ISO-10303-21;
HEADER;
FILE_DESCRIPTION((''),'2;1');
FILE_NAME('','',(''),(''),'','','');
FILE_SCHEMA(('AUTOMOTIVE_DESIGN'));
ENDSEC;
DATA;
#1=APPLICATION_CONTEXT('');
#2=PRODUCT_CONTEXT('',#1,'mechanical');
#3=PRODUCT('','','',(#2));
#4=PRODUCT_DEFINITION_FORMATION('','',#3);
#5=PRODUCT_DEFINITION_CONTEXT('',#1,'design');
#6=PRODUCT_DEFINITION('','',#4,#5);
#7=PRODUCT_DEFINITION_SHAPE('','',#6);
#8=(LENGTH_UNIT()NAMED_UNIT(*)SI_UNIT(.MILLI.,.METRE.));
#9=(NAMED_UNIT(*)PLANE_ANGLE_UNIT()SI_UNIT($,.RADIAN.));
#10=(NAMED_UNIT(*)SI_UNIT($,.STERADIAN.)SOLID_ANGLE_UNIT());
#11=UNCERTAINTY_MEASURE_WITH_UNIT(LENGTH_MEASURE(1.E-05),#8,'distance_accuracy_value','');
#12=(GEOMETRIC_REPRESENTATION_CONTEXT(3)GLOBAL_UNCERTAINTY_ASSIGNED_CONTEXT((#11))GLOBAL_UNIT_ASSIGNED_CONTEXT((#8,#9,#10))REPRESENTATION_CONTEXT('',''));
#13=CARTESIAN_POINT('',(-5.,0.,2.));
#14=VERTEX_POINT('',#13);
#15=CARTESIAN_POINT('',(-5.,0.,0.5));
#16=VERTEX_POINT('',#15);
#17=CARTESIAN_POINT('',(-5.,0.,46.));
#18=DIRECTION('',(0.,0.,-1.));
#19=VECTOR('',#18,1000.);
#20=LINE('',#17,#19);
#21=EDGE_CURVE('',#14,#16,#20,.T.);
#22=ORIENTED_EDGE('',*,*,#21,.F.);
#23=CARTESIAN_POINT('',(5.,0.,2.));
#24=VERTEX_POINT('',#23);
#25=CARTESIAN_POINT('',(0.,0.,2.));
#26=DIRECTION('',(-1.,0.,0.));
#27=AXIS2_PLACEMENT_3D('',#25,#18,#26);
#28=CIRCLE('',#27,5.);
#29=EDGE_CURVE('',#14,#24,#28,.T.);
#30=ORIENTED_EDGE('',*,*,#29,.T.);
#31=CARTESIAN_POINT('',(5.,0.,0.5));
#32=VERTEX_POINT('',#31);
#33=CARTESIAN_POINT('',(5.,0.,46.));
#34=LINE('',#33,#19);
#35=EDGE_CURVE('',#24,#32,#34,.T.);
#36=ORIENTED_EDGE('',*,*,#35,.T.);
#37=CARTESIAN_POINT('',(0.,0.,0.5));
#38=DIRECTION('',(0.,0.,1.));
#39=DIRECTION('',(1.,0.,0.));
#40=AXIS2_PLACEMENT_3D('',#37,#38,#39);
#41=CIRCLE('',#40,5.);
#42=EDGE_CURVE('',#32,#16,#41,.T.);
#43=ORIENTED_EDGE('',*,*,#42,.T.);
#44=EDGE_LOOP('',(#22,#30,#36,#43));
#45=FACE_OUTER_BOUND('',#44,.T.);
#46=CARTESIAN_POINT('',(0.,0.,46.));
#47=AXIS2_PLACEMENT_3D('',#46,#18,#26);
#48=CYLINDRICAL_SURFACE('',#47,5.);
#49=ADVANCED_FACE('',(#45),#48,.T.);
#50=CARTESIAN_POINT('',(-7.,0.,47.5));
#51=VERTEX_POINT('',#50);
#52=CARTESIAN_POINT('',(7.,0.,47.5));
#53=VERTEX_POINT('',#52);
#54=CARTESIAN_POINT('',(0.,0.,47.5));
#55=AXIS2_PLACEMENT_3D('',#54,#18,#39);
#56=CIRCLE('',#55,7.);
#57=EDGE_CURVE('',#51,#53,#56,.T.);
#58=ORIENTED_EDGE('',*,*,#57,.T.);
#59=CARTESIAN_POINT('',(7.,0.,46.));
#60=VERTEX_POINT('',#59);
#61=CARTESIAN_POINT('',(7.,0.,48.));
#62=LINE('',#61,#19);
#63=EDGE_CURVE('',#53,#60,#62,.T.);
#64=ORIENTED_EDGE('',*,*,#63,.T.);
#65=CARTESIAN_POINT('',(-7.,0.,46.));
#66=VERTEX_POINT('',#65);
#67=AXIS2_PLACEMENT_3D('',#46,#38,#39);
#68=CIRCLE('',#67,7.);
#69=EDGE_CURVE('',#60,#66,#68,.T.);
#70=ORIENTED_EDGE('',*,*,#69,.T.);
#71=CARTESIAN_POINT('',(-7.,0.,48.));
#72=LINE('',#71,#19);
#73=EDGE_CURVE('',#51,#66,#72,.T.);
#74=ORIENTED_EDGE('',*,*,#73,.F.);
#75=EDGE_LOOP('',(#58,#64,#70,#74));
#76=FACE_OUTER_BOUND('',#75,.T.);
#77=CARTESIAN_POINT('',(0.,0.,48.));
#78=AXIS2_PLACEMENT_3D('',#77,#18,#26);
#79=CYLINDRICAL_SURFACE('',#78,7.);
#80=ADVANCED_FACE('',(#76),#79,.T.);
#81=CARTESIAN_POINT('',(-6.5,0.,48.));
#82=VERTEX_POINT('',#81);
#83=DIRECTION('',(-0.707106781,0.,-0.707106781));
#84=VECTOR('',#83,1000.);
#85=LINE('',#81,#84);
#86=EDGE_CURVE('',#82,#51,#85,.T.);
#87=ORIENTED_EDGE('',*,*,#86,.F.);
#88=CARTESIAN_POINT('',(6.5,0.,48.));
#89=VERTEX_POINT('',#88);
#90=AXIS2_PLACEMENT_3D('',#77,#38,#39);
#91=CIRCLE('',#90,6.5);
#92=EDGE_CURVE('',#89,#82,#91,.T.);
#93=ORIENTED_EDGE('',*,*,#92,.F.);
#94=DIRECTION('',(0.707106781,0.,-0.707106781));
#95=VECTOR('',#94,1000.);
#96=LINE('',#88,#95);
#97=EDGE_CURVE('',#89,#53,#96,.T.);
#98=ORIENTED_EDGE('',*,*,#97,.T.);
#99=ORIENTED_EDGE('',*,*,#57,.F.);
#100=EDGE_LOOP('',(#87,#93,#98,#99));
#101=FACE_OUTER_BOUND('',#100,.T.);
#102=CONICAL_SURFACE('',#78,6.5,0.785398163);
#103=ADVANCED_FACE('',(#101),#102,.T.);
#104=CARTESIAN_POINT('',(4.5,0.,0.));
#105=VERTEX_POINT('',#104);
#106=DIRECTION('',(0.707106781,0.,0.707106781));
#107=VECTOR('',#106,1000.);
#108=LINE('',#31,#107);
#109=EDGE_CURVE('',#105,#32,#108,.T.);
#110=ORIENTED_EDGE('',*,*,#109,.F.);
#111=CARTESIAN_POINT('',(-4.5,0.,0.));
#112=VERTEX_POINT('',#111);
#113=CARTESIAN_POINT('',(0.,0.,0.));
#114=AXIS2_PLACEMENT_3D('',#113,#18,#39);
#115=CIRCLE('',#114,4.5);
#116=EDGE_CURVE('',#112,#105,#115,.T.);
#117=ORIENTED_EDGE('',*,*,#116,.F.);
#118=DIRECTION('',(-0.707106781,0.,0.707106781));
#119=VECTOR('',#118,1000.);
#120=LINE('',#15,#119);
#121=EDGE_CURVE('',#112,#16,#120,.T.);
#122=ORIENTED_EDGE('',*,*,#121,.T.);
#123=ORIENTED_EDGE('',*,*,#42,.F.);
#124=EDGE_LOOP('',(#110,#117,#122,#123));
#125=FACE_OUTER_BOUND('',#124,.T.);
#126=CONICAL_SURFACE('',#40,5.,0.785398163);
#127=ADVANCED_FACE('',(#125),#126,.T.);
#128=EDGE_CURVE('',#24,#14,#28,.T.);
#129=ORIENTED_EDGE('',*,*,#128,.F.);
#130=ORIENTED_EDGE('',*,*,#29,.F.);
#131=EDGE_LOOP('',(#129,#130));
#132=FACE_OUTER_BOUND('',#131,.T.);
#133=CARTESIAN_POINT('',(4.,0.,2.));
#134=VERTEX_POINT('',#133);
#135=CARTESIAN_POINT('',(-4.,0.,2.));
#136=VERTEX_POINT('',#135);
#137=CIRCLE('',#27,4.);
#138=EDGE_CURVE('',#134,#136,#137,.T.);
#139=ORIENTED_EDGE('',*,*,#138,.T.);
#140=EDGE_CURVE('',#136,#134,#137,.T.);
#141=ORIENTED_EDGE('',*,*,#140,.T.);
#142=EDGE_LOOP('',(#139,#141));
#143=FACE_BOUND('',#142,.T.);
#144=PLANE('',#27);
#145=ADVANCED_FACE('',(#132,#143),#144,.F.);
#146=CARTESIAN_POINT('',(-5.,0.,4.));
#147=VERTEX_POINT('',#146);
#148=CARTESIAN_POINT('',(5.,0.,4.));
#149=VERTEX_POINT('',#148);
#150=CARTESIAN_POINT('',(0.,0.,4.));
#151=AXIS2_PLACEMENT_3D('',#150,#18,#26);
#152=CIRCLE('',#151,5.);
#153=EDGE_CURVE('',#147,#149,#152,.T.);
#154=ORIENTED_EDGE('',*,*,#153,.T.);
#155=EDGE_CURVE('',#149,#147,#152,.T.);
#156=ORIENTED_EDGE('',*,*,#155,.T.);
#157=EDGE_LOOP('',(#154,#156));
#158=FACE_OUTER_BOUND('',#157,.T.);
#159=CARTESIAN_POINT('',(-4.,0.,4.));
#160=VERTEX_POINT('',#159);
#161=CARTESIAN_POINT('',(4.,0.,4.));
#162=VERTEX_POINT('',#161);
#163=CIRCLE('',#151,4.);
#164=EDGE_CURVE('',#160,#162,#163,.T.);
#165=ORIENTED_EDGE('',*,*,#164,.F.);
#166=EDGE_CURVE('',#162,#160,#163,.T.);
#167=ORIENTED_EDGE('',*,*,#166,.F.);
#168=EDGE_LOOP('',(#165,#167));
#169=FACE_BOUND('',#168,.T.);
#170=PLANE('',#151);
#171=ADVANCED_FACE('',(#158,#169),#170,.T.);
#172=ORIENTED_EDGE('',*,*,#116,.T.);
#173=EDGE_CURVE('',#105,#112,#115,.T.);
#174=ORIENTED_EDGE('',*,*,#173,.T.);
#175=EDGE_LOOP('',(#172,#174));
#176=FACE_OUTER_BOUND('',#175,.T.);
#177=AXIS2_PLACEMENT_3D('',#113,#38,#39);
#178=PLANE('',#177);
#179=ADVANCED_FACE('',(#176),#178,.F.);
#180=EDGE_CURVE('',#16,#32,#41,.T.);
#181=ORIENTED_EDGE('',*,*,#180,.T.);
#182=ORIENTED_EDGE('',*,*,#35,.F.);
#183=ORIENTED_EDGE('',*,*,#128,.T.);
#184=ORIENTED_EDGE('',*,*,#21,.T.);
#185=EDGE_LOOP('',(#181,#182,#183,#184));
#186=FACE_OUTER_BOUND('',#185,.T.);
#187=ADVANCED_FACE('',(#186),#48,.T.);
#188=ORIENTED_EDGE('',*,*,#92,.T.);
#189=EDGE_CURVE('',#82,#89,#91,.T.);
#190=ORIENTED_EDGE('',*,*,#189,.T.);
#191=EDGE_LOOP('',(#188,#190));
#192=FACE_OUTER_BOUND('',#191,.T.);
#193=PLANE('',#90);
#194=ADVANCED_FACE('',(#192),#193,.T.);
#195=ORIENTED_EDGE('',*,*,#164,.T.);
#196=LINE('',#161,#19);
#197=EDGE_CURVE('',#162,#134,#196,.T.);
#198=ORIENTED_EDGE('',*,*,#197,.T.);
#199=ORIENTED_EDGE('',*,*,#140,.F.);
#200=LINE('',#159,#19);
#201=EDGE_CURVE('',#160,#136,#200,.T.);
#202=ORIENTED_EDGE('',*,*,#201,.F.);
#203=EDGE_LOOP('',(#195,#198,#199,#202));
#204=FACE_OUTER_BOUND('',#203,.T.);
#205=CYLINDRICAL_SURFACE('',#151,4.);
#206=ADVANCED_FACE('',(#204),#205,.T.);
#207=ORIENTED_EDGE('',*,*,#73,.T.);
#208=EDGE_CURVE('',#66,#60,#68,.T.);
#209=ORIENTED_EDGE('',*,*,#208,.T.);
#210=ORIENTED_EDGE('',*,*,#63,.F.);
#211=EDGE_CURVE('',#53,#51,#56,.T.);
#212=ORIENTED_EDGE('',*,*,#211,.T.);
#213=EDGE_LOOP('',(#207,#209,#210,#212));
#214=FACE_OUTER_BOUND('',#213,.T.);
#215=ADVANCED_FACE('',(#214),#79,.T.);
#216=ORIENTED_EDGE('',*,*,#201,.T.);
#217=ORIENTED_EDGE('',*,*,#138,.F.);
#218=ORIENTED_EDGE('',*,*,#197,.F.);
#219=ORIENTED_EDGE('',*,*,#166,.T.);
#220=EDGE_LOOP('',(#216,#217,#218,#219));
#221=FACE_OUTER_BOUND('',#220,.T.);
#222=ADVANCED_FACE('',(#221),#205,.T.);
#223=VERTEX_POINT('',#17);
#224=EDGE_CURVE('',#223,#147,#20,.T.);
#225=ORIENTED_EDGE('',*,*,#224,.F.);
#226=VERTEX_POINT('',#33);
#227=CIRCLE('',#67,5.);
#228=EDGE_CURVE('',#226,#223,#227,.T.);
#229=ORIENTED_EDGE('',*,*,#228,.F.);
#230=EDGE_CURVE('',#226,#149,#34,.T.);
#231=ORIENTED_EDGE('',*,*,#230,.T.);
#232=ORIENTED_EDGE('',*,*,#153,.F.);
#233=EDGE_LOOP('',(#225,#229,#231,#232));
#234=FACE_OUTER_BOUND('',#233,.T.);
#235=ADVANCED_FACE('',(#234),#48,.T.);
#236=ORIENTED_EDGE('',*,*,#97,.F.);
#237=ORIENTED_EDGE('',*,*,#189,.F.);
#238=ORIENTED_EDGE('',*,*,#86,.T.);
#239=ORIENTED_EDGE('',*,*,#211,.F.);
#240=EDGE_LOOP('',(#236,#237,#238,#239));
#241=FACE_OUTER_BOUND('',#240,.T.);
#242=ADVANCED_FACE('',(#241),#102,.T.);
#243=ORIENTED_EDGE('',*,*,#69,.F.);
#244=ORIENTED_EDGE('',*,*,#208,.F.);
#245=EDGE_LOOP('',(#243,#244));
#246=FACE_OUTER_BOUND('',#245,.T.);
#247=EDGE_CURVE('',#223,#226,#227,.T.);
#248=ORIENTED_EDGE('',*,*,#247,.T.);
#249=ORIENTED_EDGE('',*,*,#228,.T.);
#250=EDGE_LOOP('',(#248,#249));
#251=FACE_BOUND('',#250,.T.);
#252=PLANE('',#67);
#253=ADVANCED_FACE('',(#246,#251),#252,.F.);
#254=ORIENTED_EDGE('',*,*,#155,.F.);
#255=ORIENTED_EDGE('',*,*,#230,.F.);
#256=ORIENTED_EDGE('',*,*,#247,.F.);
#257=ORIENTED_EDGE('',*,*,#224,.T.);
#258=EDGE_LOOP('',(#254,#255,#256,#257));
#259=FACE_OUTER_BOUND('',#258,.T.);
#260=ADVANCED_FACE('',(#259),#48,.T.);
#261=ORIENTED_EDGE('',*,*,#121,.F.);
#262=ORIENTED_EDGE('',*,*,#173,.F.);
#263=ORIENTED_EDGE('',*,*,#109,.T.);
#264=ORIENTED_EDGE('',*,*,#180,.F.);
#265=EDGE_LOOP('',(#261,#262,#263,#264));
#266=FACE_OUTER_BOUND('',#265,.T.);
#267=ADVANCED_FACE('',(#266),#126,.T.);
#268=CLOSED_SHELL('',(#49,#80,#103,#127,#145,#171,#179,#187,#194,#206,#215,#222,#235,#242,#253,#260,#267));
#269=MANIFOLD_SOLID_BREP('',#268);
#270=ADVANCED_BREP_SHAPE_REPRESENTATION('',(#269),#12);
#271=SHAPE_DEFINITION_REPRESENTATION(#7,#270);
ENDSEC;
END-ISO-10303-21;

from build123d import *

# Parameters (mm, degrees)
SKETCH1_R               = 5
BOSS_EXTRUDE1_DEPTH     = 46
SKETCH2_R               = 7
BOSS_EXTRUDE2_DEPTH     = 2
CHAMFER1_SIZE           = 0.5
SKETCH3_R               = 14
SKETCH3_R_2             = 4
CUT_EXTRUDE_THIN1_DEPTH = 2


with BuildPart() as part:
    # Sketch1 → Boss-Extrude1 (new body)
    with BuildSketch(Plane.XY):
        Circle(SKETCH1_R)
    extrude(amount=BOSS_EXTRUDE1_DEPTH)

    # Sketch2 → Boss-Extrude2 (add)
    with BuildSketch(Plane.XY.offset(46)):
        Circle(SKETCH2_R)
    extrude(amount=BOSS_EXTRUDE2_DEPTH)

    # Chamfer1
    chamfer1_edges = [part.edges().sort_by_distance(p)[0] for p in [
        (-5, 0, 0),
        (-7, 0, 48),
    ]]
    chamfer(chamfer1_edges, length=CHAMFER1_SIZE)

    # Sketch3 → Cut-Extrude-Thin1 (cut)
    with BuildSketch(Plane(origin=(0, 0, 2), x_dir=(-1, 0, 0), z_dir=(0, 0, -1))):
        Circle(SKETCH3_R)
        Circle(SKETCH3_R_2, mode=Mode.SUBTRACT)
    extrude(amount=-CUT_EXTRUDE_THIN1_DEPTH, mode=Mode.SUBTRACT)


solid = part.part
